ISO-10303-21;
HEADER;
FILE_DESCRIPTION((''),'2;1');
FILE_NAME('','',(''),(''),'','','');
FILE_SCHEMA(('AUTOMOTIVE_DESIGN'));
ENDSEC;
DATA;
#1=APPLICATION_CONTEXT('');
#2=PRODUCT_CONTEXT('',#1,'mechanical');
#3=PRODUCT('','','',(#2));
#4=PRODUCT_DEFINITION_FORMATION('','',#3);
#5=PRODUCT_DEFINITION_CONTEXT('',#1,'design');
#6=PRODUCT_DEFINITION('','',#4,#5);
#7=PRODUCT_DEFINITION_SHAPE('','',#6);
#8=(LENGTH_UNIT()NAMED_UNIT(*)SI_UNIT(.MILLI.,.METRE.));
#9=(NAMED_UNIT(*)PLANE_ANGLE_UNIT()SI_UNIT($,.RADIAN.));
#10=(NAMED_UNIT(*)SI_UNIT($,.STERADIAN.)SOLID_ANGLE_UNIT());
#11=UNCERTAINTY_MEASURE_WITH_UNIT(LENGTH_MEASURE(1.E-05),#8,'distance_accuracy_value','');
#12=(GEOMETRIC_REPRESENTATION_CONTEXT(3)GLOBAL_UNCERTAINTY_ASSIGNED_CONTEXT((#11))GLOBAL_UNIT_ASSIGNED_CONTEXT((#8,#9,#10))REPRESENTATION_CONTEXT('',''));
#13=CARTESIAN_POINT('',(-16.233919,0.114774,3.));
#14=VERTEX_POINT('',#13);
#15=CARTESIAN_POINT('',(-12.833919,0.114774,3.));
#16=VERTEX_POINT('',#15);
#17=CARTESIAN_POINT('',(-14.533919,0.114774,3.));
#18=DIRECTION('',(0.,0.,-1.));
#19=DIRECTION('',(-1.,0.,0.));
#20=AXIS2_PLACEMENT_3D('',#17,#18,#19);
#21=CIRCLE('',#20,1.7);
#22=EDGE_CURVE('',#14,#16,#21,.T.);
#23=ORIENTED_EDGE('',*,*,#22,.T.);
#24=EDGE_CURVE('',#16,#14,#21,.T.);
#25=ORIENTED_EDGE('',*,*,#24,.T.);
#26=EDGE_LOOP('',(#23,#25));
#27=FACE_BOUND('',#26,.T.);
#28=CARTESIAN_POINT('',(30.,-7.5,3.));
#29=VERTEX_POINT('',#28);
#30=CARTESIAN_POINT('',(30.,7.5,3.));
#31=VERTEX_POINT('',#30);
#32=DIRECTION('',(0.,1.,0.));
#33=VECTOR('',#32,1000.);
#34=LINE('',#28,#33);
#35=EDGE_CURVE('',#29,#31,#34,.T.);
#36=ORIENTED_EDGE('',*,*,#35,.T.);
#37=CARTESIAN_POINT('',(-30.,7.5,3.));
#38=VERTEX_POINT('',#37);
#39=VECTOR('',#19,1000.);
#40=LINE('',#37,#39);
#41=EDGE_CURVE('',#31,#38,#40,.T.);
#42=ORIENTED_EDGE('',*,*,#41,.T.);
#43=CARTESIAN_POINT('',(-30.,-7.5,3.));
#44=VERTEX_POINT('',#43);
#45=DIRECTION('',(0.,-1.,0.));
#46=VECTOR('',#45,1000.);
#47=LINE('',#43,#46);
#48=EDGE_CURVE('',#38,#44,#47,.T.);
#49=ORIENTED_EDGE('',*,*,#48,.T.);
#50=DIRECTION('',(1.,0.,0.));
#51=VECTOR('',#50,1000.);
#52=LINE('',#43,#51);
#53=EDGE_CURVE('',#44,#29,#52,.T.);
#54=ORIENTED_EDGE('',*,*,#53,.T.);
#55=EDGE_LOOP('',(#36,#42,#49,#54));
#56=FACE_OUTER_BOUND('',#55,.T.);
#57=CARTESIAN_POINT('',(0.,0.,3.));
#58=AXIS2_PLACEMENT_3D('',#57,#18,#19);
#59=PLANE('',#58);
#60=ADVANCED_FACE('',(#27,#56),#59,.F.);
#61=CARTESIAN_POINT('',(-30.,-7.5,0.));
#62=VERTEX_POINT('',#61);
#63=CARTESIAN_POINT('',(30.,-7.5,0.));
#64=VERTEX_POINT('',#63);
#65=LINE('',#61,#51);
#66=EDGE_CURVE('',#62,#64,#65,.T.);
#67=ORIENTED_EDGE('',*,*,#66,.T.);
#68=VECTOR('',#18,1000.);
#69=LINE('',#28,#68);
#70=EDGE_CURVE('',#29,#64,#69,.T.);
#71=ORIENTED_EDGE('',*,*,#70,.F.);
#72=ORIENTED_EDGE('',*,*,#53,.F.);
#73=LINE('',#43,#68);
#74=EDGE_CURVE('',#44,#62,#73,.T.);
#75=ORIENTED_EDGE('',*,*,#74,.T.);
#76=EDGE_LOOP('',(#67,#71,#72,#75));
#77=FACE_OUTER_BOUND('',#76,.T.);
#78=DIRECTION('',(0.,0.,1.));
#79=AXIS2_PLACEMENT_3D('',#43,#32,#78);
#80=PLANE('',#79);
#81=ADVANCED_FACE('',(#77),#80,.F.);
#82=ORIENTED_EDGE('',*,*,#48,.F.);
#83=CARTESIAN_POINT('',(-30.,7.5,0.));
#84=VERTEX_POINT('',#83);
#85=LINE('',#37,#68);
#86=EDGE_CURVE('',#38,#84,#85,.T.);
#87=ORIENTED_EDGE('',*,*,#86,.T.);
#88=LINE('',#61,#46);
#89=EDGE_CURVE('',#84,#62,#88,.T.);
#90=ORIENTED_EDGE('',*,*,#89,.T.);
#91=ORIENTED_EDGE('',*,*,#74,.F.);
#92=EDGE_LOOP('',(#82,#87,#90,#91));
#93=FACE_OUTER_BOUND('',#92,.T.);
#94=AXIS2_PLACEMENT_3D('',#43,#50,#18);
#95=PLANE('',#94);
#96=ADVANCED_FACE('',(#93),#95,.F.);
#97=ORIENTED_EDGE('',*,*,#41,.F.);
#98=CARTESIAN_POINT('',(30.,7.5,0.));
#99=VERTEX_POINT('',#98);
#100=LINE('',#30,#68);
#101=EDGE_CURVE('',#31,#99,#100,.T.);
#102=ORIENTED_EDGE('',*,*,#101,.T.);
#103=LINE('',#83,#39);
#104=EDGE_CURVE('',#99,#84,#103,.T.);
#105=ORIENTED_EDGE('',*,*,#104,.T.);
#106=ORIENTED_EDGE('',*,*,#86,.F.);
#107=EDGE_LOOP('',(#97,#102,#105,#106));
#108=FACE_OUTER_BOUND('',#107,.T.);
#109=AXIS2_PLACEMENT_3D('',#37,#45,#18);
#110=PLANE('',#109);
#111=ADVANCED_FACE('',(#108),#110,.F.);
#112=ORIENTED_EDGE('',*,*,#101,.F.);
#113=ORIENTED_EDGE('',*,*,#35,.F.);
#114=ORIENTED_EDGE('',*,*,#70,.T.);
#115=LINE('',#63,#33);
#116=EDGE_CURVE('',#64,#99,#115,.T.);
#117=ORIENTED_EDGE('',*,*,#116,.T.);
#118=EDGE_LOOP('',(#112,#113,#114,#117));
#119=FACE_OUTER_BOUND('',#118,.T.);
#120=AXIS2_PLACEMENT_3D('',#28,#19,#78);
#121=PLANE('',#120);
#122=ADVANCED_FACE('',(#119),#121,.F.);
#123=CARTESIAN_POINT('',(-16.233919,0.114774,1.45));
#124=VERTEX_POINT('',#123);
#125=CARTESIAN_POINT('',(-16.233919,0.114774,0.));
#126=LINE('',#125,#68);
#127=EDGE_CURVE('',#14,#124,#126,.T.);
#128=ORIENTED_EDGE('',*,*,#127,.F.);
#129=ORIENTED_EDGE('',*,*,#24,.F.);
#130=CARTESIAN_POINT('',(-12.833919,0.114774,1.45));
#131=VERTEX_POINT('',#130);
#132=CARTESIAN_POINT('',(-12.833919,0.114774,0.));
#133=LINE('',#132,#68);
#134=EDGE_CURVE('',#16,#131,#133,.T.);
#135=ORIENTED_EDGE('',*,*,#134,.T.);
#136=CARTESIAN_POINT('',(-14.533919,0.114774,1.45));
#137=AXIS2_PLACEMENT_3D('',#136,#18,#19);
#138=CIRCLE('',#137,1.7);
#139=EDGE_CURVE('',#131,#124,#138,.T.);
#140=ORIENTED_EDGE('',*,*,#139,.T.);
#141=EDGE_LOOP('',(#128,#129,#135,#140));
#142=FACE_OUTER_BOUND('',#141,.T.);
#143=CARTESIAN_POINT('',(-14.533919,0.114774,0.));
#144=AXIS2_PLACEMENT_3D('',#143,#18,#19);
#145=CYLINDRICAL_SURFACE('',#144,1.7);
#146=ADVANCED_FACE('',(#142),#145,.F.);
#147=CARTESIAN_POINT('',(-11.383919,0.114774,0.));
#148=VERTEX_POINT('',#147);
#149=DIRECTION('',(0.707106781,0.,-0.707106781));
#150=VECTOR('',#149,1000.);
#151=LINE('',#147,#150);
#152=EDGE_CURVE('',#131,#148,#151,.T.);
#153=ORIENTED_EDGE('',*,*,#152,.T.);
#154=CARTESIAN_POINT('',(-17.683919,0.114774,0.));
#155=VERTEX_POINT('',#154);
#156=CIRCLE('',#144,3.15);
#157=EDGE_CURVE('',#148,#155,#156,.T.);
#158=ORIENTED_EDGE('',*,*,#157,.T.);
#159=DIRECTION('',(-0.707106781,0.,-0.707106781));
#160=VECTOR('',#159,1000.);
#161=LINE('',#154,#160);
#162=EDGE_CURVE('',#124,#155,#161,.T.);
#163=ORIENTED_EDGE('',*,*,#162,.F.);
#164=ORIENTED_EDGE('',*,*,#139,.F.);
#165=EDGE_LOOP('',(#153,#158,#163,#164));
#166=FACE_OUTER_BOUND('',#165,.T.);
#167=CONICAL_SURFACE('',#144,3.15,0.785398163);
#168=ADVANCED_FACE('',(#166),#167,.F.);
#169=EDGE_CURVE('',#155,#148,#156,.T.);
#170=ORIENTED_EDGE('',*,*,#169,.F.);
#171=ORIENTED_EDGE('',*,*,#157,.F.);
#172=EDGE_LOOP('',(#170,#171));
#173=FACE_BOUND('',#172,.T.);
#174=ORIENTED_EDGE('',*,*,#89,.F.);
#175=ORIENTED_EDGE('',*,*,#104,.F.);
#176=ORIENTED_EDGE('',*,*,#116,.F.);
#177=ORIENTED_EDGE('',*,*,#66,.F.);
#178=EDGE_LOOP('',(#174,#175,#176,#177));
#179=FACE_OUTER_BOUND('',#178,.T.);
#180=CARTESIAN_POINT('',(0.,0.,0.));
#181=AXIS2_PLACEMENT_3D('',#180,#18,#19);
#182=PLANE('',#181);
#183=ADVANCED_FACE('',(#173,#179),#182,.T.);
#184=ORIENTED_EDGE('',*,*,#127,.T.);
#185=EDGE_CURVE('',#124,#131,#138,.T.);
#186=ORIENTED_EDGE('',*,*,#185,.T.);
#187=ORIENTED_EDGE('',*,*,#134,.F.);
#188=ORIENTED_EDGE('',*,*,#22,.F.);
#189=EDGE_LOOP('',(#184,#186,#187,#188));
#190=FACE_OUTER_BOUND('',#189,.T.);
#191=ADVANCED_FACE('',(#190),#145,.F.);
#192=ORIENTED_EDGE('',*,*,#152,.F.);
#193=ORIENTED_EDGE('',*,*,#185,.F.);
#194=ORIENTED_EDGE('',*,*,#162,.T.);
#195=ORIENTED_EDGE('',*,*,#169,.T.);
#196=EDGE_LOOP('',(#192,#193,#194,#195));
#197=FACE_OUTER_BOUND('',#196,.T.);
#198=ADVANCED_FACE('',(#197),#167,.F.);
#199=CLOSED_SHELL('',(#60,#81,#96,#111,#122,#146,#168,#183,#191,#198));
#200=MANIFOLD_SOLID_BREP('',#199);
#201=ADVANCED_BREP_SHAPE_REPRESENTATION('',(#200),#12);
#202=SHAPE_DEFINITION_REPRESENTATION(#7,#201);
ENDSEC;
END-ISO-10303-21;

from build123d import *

# Parameters (mm, degrees)
SKETCH_1_W      = 60
SKETCH_1_H      = 15
EXTRUDE_1_DEPTH = 3


with BuildPart() as part:
    # 草图1 → 凸台-拉伸1 (new body)
    with BuildSketch(Plane.XY):
        Rectangle(SKETCH_1_W, SKETCH_1_H)
    extrude(amount=EXTRUDE_1_DEPTH)

    # 草图2 → M3 十字切槽平头螺钉锥孔1 (revolve, cut)
    with BuildSketch(Plane(origin=(-14.533919383, 0.114773803, 0), x_dir=(0, 1, 0), z_dir=(1, 0, 0))):
        Polygon((0, 0), (0, 3), (1.7, 3), (1.7, 1.45), (3.15, 0), align=None)
    revolve(axis=Axis((-14.533919383, 0.114773803, -6.35), (0, 0, 1)), mode=Mode.SUBTRACT)


solid = part.part
